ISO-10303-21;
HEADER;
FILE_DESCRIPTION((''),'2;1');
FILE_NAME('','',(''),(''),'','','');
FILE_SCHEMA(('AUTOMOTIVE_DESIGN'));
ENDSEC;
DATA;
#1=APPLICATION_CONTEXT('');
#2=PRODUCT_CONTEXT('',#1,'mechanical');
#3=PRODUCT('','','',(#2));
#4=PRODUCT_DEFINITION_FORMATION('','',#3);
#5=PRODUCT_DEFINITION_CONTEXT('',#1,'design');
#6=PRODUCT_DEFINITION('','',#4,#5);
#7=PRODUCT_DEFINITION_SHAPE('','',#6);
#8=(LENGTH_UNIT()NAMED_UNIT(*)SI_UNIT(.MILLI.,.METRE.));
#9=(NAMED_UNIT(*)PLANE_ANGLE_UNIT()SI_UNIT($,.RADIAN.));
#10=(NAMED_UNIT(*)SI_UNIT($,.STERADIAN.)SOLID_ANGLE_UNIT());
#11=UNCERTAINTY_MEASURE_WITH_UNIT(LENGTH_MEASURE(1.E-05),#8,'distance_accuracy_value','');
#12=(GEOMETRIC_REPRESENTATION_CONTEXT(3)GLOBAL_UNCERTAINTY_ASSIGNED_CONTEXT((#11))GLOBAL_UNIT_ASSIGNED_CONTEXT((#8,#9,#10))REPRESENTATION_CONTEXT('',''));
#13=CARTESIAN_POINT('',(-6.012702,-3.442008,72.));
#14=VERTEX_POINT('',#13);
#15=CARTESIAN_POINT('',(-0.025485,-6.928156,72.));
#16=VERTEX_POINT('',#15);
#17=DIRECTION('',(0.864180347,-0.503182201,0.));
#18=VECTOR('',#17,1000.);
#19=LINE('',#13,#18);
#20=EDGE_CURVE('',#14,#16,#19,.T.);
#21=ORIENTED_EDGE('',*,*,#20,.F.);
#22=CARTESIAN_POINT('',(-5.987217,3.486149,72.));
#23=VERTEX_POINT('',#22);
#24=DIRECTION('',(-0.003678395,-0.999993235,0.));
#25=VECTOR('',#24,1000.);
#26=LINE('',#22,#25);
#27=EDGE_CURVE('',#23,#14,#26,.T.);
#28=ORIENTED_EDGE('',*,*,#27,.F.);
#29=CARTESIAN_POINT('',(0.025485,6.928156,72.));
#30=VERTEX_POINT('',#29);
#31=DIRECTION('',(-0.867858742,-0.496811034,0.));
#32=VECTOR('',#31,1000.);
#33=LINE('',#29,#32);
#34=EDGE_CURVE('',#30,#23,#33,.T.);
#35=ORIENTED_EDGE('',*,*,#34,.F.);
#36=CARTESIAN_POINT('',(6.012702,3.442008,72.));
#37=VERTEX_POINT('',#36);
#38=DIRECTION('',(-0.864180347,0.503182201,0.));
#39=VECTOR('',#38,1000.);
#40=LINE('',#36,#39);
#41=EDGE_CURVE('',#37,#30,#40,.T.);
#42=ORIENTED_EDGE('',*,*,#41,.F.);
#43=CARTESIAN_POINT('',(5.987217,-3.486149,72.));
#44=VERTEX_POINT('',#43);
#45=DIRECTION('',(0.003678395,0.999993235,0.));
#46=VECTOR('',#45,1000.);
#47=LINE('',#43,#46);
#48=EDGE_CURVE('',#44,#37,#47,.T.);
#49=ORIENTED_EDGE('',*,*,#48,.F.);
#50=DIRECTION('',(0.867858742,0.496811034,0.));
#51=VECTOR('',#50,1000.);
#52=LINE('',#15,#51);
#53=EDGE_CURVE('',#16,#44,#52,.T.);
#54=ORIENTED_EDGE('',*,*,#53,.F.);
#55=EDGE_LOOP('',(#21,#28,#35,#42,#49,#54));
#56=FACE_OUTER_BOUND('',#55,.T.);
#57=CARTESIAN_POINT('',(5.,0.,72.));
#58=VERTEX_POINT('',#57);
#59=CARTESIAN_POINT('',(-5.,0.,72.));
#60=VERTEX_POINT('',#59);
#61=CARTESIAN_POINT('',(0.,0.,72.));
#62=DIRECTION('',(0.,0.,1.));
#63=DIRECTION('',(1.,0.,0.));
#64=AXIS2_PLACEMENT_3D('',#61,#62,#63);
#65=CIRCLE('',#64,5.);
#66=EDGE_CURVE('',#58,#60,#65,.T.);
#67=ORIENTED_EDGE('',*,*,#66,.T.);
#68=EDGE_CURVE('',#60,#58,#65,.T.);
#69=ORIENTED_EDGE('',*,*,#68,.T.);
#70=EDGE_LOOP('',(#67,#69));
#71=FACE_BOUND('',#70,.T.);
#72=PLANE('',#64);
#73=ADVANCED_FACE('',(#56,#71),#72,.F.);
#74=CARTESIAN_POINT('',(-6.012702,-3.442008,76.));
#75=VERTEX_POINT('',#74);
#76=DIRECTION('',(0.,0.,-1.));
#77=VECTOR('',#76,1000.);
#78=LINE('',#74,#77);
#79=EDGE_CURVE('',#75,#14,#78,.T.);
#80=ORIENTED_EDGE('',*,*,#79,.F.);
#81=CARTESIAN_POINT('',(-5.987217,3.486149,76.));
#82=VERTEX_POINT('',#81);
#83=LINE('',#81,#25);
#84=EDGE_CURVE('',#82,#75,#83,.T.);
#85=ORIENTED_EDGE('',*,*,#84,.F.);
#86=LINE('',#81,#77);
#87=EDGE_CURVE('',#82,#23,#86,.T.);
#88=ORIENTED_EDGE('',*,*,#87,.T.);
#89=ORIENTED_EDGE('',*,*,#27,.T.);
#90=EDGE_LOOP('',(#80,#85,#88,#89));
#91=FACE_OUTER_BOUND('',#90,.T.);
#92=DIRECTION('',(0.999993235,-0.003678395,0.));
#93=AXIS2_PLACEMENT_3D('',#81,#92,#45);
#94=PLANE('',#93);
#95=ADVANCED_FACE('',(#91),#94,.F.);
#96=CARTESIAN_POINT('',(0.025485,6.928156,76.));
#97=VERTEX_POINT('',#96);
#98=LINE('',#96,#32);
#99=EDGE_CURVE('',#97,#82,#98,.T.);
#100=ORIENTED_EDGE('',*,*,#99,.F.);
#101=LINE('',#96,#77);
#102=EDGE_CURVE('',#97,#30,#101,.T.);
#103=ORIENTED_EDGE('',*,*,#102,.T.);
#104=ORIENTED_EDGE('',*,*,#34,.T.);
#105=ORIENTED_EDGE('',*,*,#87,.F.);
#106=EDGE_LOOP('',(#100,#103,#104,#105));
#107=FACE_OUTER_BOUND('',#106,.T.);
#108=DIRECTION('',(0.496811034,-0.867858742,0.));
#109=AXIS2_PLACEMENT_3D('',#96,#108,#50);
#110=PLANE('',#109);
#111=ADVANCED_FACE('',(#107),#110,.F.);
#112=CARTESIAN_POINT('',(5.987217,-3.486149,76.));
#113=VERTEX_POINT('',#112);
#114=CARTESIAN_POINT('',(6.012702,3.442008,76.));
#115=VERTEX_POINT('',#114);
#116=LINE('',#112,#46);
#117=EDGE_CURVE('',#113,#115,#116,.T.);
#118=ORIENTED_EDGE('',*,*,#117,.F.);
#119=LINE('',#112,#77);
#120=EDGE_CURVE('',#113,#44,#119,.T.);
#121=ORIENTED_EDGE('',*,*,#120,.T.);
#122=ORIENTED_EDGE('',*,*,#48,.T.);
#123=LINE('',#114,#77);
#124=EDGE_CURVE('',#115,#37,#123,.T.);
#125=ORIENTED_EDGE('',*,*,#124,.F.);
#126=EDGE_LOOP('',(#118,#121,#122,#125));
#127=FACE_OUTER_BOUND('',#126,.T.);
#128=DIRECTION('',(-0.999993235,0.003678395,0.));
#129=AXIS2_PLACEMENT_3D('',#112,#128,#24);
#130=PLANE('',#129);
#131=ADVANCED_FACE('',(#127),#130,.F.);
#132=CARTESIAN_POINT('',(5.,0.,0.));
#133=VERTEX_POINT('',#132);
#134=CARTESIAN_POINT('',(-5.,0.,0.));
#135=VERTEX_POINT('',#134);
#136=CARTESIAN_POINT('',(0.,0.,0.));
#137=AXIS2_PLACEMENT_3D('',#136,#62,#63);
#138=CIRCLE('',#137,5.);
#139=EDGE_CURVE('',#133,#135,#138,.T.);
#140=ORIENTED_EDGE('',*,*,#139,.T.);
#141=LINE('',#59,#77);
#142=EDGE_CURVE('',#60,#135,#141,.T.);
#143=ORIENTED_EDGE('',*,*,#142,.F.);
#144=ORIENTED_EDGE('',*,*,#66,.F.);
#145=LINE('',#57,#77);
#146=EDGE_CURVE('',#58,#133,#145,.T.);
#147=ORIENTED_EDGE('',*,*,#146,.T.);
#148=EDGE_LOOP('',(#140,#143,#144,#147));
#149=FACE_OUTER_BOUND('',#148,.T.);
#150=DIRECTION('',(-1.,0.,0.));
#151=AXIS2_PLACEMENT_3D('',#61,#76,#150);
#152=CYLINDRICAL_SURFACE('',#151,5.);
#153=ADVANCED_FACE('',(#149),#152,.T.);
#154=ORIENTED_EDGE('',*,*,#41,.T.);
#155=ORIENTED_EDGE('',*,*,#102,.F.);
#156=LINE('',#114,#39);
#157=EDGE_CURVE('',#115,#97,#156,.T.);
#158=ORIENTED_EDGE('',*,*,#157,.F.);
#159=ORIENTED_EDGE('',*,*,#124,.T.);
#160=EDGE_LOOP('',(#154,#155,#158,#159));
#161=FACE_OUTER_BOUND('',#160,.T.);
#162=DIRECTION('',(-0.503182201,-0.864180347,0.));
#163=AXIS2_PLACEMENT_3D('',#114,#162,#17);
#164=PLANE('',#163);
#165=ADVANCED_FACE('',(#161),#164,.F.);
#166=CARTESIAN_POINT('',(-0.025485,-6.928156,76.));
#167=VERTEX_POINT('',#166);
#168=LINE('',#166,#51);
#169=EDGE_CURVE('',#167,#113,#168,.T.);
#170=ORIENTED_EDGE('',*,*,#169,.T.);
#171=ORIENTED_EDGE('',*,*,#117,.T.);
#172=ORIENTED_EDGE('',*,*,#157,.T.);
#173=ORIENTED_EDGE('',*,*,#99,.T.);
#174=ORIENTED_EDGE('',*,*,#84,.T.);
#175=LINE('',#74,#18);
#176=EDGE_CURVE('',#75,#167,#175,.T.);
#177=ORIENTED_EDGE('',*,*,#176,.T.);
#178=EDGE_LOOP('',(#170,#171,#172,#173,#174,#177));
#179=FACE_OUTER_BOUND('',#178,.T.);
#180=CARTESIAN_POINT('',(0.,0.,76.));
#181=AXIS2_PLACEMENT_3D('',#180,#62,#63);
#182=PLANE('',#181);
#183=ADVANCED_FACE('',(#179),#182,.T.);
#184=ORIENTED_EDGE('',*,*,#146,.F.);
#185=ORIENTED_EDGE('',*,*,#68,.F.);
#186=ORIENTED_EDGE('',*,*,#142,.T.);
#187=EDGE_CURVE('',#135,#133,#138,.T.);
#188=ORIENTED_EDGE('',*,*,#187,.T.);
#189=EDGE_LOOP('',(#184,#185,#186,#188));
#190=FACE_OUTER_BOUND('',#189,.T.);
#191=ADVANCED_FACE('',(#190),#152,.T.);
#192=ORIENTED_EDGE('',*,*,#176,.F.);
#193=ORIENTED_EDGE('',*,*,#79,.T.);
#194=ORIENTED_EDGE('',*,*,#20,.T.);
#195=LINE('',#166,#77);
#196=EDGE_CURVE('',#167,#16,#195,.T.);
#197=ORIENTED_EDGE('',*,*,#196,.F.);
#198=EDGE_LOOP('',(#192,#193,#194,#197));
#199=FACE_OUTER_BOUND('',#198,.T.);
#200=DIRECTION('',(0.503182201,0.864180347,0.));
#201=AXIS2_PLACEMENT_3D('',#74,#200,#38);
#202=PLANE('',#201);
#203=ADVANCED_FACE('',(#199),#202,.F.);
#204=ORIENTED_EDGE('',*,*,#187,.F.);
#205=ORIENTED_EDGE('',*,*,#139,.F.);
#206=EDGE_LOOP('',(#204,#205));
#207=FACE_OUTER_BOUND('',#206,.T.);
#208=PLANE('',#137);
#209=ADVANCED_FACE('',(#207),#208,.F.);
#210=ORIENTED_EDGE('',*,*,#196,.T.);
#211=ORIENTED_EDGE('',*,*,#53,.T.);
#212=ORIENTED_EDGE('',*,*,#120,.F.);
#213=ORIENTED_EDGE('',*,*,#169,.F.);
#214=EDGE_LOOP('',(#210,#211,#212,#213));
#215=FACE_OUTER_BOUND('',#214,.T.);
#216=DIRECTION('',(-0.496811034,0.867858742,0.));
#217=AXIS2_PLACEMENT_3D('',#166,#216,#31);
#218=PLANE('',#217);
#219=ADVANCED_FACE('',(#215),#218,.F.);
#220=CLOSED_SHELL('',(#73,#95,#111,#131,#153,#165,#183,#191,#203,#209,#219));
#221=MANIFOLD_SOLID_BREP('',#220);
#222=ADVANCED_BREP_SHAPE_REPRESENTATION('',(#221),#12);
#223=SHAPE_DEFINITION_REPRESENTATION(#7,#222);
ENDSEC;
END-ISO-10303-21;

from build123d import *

# Parameters (mm, degrees)
SKETCH_1_R      = 5
EXTRUDE_1_DEPTH = 72
EXTRUDE_2_DEPTH = 4


with BuildPart() as part:
    # 草图1 → 凸台-拉伸1 (new body)
    with BuildSketch(Plane.XY):
        Circle(SKETCH_1_R)
    extrude(amount=EXTRUDE_1_DEPTH)

    # 草图2 → 凸台-拉伸2 (add)
    with BuildSketch(Plane.XY.offset(72)):
        Polygon((5.987217074, -3.486148549), (6.012701742, 3.44200781), (0.025484667, 6.928156359), (-5.987217074, 3.486148549), (-6.012701742, -3.44200781), (-0.025484667, -6.928156359), align=None)
    extrude(amount=EXTRUDE_2_DEPTH)


solid = part.part
